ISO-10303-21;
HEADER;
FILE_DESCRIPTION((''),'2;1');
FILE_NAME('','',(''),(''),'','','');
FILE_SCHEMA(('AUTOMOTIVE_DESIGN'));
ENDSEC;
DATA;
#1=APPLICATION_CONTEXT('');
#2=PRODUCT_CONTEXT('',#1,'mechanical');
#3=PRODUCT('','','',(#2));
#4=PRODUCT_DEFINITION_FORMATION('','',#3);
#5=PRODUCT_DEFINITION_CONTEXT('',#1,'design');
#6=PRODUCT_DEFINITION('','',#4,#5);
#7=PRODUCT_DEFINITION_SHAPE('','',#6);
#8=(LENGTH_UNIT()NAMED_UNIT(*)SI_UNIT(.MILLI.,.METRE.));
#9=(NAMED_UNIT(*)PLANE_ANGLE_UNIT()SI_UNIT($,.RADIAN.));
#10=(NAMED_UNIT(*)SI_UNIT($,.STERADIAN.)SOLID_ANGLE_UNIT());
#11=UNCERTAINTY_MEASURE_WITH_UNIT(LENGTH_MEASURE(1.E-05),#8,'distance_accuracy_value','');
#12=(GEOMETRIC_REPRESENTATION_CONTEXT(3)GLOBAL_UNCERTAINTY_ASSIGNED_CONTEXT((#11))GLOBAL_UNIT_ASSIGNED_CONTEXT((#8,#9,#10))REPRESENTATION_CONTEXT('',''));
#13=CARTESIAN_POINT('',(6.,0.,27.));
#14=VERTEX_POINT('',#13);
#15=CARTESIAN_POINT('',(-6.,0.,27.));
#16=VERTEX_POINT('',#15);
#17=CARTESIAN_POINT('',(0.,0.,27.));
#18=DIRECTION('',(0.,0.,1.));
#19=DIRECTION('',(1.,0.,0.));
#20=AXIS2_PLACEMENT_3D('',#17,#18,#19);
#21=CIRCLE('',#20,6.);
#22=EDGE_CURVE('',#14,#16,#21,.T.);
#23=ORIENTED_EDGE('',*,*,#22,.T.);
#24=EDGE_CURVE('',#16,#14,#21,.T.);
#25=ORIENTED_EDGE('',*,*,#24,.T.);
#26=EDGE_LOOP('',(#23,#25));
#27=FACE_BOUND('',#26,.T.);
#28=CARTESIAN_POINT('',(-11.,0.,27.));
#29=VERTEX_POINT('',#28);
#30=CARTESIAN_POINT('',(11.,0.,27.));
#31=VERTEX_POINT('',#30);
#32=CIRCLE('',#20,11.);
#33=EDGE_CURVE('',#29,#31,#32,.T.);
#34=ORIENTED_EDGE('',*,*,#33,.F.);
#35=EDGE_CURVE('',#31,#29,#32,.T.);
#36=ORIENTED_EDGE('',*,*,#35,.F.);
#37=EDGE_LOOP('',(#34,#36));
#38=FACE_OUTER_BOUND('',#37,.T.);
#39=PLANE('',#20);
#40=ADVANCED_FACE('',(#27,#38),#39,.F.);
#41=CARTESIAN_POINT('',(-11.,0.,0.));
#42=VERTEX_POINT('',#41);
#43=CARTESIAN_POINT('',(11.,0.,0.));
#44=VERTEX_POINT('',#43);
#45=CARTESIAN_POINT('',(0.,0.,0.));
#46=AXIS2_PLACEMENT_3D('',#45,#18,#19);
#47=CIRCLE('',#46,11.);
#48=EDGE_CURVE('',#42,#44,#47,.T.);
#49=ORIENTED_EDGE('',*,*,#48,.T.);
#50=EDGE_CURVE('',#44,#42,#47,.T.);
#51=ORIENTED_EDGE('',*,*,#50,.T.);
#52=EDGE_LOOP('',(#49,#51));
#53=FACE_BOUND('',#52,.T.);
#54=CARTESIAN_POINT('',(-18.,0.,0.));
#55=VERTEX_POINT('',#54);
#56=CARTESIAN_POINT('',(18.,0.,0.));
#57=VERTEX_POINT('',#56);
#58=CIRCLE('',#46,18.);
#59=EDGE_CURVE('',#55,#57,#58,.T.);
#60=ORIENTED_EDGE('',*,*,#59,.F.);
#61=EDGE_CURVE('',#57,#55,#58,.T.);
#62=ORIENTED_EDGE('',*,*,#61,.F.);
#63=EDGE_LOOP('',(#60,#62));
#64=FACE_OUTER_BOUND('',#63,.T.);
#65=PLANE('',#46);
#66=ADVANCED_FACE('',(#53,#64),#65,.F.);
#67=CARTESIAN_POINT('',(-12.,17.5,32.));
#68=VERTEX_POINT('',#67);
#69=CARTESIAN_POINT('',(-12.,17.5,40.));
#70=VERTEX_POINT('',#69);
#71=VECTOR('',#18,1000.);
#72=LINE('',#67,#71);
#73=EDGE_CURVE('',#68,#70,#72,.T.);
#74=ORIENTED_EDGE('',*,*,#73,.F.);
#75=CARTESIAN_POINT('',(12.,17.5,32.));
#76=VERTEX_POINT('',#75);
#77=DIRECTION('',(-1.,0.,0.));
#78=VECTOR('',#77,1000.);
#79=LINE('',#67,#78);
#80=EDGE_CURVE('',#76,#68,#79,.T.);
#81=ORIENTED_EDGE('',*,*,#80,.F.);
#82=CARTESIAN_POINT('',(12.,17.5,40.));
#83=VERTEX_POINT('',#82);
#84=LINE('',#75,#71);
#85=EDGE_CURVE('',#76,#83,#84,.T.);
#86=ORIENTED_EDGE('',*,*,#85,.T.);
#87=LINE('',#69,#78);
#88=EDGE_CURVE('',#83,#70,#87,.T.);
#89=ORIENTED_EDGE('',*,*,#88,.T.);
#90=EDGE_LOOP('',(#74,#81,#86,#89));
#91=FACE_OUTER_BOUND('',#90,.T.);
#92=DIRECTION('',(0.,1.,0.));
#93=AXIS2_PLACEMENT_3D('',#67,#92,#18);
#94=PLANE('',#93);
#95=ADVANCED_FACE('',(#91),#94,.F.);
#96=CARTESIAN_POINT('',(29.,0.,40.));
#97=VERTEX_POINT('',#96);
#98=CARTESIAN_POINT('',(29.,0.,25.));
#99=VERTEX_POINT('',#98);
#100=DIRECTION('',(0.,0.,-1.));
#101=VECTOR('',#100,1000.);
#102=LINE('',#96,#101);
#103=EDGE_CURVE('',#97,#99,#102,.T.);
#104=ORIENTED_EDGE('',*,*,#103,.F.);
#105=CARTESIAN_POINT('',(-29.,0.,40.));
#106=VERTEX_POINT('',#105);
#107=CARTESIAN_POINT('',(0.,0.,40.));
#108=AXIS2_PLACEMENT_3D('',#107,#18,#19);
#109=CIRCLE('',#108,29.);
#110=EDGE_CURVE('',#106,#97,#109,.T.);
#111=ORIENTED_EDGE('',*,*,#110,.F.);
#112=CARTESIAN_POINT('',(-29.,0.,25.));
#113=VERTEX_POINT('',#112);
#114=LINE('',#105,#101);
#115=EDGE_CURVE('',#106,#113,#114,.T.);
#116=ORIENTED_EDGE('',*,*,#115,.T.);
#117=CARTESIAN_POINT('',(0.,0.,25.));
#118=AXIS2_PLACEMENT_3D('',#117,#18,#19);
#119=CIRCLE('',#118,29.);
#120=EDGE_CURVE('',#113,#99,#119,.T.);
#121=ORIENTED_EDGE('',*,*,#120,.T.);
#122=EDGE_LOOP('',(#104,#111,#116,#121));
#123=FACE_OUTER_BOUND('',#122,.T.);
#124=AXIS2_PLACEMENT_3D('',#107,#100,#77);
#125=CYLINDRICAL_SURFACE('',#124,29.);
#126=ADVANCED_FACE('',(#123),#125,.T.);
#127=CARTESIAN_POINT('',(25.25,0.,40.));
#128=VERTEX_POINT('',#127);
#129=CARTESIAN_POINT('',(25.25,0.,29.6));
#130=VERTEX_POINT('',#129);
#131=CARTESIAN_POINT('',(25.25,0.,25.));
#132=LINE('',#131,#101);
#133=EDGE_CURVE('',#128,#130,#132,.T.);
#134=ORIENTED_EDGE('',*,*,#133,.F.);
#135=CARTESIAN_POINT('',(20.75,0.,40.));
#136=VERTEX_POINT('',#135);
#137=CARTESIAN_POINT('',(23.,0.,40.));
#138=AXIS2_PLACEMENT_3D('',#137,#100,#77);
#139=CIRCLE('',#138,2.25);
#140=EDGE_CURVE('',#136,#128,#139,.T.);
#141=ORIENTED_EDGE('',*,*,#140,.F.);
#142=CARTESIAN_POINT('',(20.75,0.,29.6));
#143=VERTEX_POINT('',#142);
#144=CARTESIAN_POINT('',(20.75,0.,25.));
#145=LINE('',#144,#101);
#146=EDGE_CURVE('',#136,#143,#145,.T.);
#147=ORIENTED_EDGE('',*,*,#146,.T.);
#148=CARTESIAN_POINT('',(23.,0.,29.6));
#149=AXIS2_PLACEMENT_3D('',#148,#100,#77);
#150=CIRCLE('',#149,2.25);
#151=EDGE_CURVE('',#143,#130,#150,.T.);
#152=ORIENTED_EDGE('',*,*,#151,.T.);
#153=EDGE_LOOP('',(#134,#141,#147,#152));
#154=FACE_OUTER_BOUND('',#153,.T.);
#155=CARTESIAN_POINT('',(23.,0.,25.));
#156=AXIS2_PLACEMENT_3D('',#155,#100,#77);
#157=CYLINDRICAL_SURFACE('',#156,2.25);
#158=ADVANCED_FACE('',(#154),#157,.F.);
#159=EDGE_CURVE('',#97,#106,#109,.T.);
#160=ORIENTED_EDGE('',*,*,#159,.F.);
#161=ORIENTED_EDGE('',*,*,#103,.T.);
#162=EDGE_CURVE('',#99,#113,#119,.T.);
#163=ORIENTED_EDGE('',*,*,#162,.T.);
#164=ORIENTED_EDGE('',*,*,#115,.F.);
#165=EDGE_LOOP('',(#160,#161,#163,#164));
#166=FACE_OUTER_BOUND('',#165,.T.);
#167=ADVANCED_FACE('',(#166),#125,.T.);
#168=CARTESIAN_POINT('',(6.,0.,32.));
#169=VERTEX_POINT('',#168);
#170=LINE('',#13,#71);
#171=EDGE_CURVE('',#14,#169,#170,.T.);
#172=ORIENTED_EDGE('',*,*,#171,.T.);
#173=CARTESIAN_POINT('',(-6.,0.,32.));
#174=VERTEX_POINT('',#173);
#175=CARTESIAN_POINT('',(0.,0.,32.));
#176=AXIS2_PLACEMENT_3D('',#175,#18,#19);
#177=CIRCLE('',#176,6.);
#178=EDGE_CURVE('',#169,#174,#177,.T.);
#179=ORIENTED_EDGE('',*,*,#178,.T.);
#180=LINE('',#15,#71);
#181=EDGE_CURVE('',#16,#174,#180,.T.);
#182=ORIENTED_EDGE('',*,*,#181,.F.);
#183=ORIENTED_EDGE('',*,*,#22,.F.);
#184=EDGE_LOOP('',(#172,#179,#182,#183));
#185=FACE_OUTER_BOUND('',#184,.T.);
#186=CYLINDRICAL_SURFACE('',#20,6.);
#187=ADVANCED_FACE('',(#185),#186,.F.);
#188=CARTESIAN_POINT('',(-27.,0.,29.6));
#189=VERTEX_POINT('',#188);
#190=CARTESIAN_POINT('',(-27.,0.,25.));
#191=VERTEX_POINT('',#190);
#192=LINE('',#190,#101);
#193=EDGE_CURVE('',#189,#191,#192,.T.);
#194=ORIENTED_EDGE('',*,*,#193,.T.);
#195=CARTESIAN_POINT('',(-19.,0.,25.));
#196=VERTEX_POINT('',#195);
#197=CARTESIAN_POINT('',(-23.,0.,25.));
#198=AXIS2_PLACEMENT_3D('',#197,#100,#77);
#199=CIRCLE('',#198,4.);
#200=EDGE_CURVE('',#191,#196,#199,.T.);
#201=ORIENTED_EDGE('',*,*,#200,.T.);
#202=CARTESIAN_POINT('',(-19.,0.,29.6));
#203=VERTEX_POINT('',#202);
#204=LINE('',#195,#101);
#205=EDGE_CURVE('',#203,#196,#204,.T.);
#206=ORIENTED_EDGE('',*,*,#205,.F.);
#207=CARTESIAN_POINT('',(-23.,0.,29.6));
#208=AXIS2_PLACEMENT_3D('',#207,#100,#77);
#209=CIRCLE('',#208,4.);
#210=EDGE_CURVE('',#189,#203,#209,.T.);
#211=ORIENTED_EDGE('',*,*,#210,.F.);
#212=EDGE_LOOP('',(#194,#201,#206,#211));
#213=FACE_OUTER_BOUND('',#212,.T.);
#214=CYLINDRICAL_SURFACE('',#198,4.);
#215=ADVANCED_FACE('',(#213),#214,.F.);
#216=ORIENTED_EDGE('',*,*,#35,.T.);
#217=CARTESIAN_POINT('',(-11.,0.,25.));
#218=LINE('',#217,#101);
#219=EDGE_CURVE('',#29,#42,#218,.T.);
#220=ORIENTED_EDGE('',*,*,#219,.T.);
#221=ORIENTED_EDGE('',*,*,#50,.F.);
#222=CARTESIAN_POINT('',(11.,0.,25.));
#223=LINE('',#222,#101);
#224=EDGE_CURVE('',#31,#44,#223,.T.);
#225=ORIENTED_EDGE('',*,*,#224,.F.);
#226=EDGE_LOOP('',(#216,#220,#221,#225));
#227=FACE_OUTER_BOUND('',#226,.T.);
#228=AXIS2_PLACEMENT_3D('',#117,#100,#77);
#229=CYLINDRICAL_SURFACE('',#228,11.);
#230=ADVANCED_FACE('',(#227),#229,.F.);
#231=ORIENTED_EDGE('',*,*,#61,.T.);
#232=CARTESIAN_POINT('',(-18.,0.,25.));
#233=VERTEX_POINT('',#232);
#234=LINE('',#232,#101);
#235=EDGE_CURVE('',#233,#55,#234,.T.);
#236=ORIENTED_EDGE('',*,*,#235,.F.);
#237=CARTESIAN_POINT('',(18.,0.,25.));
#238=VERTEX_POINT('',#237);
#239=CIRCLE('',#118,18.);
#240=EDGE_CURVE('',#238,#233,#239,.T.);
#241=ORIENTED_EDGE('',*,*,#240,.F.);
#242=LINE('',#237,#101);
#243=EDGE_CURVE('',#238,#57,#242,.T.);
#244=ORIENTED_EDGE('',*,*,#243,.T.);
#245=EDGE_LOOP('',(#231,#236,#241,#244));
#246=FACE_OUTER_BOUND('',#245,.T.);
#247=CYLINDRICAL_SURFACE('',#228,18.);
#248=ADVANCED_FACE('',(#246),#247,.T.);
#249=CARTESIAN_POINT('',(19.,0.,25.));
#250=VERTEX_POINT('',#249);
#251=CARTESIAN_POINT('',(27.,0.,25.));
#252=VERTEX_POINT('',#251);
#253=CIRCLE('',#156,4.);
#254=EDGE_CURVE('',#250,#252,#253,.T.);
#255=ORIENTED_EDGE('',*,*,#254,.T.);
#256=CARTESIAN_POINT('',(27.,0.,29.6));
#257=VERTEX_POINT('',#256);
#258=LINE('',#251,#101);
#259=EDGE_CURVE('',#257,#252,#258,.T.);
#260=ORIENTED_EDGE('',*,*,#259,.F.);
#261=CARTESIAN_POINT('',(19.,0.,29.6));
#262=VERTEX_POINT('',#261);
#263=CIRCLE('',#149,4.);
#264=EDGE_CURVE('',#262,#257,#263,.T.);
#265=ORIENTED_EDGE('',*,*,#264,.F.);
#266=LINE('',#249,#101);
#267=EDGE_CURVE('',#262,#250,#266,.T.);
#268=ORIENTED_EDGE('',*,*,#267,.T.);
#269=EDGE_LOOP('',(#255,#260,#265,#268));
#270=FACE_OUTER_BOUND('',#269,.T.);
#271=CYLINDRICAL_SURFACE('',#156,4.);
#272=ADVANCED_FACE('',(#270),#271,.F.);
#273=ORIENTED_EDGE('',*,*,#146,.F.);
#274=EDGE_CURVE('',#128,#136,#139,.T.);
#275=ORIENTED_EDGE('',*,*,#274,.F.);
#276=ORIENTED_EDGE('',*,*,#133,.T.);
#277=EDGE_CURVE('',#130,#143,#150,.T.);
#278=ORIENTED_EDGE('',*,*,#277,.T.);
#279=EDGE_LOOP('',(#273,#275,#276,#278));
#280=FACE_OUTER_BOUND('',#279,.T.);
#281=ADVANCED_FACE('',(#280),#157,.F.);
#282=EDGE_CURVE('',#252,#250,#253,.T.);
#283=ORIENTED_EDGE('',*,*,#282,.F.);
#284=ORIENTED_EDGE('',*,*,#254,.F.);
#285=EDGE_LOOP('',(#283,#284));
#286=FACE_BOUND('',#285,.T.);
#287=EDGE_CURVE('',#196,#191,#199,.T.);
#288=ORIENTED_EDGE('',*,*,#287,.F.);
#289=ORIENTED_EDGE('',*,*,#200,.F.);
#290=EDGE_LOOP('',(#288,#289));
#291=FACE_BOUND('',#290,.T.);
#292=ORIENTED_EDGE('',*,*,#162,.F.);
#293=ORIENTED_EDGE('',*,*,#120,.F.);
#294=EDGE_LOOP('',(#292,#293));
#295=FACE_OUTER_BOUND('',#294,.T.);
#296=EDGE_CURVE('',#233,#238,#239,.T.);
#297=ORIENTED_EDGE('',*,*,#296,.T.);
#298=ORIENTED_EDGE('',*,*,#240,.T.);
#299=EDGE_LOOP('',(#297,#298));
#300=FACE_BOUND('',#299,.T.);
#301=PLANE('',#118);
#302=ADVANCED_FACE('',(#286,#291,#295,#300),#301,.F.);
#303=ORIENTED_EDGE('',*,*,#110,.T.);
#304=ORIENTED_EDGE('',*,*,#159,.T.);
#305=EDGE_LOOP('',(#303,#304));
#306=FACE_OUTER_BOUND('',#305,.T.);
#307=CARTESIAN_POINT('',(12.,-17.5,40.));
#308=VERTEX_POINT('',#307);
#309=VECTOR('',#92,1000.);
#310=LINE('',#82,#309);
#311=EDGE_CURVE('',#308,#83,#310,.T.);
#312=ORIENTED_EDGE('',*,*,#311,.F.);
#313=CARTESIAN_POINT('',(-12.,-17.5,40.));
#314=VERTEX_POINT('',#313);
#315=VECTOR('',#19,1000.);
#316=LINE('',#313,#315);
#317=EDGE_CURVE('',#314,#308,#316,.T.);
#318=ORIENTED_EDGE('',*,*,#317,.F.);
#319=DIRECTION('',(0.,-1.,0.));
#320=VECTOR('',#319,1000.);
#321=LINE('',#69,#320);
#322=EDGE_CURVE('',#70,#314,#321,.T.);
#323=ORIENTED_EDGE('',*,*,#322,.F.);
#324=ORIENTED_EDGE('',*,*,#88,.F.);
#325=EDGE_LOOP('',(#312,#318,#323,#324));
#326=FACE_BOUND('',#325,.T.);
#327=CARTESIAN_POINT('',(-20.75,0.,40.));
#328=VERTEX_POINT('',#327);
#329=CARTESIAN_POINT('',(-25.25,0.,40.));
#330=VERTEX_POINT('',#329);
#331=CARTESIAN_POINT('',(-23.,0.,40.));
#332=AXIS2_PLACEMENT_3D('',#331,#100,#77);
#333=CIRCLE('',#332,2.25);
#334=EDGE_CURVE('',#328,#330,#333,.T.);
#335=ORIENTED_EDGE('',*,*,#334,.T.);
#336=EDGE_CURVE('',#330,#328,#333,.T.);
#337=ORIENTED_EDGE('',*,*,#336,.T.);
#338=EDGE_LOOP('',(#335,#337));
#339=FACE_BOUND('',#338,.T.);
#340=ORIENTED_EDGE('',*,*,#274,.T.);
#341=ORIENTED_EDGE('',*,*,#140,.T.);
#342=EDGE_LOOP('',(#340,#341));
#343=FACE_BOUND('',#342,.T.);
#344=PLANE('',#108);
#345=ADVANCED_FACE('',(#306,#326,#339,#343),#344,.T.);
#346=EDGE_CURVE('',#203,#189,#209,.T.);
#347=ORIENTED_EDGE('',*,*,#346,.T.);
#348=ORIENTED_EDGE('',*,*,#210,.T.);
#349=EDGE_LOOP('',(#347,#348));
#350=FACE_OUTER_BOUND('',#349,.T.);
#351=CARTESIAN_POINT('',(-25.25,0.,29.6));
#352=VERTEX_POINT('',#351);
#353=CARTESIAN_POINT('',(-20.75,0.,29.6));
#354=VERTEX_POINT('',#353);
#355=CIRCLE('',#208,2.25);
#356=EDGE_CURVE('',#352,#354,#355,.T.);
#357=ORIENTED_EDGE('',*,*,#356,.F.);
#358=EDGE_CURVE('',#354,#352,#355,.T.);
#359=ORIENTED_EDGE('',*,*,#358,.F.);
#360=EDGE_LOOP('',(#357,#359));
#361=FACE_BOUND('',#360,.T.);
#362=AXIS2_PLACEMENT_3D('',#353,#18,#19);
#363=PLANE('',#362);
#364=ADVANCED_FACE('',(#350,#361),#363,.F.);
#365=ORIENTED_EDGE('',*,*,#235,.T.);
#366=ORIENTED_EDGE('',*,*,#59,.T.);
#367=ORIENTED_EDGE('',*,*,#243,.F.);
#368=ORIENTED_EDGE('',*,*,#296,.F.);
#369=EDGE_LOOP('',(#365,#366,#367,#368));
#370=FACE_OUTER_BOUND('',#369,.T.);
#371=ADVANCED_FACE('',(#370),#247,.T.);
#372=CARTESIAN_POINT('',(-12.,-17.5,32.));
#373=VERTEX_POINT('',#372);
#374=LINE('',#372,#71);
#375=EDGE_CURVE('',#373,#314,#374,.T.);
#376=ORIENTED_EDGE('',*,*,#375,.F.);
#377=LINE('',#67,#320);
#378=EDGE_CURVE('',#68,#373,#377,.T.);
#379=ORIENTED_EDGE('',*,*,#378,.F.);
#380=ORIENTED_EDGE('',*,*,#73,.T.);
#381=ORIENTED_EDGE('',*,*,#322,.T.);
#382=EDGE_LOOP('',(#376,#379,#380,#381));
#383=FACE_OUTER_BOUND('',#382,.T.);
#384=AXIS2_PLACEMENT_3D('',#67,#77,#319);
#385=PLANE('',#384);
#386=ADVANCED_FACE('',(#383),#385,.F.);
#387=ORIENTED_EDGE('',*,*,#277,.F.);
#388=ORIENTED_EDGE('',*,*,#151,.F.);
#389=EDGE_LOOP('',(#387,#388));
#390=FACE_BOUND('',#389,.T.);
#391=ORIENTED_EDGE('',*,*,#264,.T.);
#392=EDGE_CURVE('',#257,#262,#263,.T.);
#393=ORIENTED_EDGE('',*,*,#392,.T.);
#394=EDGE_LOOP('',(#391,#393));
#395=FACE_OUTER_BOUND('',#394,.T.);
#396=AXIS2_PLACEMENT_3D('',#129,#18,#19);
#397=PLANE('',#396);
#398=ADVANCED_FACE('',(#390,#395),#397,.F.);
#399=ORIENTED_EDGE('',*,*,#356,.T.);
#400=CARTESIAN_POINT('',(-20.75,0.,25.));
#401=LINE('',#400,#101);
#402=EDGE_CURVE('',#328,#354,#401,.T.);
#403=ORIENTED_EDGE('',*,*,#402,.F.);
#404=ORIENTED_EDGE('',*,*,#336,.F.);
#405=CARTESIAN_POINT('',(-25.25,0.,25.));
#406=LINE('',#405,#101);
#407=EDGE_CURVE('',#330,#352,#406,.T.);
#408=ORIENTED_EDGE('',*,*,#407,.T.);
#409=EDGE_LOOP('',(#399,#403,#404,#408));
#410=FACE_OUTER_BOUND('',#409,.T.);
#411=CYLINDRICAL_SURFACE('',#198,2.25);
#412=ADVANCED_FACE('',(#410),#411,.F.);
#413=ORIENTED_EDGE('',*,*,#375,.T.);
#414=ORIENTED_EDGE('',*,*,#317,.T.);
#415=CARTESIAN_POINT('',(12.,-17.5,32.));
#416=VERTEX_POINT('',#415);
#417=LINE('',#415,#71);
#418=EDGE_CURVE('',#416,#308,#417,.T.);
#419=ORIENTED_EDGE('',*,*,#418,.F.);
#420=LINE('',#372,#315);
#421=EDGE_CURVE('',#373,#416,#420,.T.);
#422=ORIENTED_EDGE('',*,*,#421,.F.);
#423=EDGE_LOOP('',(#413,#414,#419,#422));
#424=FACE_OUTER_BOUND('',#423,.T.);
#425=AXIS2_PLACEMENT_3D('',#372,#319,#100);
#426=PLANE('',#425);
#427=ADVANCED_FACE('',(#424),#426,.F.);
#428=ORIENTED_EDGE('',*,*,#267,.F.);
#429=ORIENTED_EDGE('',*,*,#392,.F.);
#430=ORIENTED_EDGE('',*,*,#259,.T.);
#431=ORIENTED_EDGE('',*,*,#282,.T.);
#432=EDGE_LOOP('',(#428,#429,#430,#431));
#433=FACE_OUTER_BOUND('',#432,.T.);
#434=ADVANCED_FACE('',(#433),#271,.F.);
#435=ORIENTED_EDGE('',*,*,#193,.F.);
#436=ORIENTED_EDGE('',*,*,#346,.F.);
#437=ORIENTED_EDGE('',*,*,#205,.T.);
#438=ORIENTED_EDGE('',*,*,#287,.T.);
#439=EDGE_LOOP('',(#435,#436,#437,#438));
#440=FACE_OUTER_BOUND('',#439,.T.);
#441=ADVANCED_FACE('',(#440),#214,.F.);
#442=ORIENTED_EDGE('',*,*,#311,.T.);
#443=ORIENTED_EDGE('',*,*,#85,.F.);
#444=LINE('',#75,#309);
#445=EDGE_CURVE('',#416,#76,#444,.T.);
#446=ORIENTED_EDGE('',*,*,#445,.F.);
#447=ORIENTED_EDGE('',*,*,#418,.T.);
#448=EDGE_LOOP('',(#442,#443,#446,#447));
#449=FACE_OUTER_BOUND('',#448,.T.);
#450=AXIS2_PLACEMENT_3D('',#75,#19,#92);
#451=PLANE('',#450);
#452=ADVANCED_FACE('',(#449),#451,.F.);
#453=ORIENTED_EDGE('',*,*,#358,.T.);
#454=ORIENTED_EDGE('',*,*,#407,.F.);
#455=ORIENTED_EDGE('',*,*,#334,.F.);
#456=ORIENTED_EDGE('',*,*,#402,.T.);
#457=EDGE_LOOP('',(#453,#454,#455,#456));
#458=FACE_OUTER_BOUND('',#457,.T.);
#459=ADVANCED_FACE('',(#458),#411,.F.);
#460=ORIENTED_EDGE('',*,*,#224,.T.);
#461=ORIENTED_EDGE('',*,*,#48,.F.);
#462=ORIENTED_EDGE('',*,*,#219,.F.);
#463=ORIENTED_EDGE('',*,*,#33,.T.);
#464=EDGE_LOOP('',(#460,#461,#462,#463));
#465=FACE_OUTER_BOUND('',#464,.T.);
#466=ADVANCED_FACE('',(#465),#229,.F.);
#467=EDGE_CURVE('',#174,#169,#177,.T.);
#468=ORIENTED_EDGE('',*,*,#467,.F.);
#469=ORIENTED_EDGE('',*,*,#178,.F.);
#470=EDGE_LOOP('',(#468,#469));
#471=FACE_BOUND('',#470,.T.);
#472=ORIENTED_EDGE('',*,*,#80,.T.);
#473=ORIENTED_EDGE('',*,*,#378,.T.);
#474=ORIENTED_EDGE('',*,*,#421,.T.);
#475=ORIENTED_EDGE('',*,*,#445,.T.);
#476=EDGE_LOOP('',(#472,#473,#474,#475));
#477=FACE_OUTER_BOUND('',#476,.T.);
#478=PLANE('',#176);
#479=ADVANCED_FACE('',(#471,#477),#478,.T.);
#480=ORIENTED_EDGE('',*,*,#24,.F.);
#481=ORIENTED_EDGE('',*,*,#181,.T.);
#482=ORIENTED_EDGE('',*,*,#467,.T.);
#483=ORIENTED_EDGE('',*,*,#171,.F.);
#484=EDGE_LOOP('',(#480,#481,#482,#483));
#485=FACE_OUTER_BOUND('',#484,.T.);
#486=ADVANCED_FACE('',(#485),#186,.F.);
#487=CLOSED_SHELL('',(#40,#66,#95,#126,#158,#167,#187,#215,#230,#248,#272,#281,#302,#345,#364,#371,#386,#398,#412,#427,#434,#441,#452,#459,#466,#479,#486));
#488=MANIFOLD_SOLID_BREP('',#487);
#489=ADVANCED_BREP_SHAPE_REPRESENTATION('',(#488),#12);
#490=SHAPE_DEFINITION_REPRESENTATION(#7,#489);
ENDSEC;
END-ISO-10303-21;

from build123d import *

# Parameters (mm, degrees)
SKETCH_1_R                = 18
SKETCH_1_R_2              = 11
EXTRUDE_1_DEPTH           = 25
SKETCH_2_R                = 29
SKETCH_2_R_2              = 11
EXTRUDE_2_DEPTH           = 15
HOLE_WIZARD_1_D           = 4.5
HOLE_WIZARD_1_CBORE_D     = 8
HOLE_WIZARD_1_CBORE_DEPTH = 4.6
SKETCH_6_W                = 24
SKETCH_6_H                = 35
CUT_EXTRUDE_1_DEPTH       = 8
EXTRUDE_START             = -5
SKETCH_7_R                = 11
SKETCH_7_R_2              = 6
EXTRUDE_3_DEPTH           = 5


with BuildPart() as part:
    # 草图1 → 凸台-拉伸1 (new body)
    with BuildSketch(Plane.XY):
        Circle(SKETCH_1_R)
        Circle(SKETCH_1_R_2, mode=Mode.SUBTRACT)
    extrude(amount=EXTRUDE_1_DEPTH)

    # 草图2 → 凸台-拉伸2 (add)
    with BuildSketch(Plane.XY.offset(25)):
        Circle(SKETCH_2_R)
        Circle(SKETCH_2_R_2, mode=Mode.SUBTRACT)
    extrude(amount=EXTRUDE_2_DEPTH)

    # 打孔尺寸根据内六角圆柱头螺钉的类型1 (through all)
    with Locations(Plane(origin=(0, 0, 25), x_dir=(-1, 0, 0), z_dir=(0, 0, -1))):
        with Locations((-23, 0), (23, 0)):
            CounterBoreHole(HOLE_WIZARD_1_D / 2, HOLE_WIZARD_1_CBORE_D / 2, HOLE_WIZARD_1_CBORE_DEPTH)

    # 草图6 → 切除-拉伸1 (cut)
    with BuildSketch(Plane.XY.offset(40)):
        Rectangle(SKETCH_6_W, SKETCH_6_H)
    extrude(amount=-CUT_EXTRUDE_1_DEPTH, mode=Mode.SUBTRACT)

    # 草图7 → 凸台-拉伸3 (add)
    with BuildSketch(Plane.XY.offset(32).offset(EXTRUDE_START)):
        Circle(SKETCH_7_R)
        Circle(SKETCH_7_R_2, mode=Mode.SUBTRACT)
    extrude(amount=EXTRUDE_3_DEPTH)


solid = part.part
